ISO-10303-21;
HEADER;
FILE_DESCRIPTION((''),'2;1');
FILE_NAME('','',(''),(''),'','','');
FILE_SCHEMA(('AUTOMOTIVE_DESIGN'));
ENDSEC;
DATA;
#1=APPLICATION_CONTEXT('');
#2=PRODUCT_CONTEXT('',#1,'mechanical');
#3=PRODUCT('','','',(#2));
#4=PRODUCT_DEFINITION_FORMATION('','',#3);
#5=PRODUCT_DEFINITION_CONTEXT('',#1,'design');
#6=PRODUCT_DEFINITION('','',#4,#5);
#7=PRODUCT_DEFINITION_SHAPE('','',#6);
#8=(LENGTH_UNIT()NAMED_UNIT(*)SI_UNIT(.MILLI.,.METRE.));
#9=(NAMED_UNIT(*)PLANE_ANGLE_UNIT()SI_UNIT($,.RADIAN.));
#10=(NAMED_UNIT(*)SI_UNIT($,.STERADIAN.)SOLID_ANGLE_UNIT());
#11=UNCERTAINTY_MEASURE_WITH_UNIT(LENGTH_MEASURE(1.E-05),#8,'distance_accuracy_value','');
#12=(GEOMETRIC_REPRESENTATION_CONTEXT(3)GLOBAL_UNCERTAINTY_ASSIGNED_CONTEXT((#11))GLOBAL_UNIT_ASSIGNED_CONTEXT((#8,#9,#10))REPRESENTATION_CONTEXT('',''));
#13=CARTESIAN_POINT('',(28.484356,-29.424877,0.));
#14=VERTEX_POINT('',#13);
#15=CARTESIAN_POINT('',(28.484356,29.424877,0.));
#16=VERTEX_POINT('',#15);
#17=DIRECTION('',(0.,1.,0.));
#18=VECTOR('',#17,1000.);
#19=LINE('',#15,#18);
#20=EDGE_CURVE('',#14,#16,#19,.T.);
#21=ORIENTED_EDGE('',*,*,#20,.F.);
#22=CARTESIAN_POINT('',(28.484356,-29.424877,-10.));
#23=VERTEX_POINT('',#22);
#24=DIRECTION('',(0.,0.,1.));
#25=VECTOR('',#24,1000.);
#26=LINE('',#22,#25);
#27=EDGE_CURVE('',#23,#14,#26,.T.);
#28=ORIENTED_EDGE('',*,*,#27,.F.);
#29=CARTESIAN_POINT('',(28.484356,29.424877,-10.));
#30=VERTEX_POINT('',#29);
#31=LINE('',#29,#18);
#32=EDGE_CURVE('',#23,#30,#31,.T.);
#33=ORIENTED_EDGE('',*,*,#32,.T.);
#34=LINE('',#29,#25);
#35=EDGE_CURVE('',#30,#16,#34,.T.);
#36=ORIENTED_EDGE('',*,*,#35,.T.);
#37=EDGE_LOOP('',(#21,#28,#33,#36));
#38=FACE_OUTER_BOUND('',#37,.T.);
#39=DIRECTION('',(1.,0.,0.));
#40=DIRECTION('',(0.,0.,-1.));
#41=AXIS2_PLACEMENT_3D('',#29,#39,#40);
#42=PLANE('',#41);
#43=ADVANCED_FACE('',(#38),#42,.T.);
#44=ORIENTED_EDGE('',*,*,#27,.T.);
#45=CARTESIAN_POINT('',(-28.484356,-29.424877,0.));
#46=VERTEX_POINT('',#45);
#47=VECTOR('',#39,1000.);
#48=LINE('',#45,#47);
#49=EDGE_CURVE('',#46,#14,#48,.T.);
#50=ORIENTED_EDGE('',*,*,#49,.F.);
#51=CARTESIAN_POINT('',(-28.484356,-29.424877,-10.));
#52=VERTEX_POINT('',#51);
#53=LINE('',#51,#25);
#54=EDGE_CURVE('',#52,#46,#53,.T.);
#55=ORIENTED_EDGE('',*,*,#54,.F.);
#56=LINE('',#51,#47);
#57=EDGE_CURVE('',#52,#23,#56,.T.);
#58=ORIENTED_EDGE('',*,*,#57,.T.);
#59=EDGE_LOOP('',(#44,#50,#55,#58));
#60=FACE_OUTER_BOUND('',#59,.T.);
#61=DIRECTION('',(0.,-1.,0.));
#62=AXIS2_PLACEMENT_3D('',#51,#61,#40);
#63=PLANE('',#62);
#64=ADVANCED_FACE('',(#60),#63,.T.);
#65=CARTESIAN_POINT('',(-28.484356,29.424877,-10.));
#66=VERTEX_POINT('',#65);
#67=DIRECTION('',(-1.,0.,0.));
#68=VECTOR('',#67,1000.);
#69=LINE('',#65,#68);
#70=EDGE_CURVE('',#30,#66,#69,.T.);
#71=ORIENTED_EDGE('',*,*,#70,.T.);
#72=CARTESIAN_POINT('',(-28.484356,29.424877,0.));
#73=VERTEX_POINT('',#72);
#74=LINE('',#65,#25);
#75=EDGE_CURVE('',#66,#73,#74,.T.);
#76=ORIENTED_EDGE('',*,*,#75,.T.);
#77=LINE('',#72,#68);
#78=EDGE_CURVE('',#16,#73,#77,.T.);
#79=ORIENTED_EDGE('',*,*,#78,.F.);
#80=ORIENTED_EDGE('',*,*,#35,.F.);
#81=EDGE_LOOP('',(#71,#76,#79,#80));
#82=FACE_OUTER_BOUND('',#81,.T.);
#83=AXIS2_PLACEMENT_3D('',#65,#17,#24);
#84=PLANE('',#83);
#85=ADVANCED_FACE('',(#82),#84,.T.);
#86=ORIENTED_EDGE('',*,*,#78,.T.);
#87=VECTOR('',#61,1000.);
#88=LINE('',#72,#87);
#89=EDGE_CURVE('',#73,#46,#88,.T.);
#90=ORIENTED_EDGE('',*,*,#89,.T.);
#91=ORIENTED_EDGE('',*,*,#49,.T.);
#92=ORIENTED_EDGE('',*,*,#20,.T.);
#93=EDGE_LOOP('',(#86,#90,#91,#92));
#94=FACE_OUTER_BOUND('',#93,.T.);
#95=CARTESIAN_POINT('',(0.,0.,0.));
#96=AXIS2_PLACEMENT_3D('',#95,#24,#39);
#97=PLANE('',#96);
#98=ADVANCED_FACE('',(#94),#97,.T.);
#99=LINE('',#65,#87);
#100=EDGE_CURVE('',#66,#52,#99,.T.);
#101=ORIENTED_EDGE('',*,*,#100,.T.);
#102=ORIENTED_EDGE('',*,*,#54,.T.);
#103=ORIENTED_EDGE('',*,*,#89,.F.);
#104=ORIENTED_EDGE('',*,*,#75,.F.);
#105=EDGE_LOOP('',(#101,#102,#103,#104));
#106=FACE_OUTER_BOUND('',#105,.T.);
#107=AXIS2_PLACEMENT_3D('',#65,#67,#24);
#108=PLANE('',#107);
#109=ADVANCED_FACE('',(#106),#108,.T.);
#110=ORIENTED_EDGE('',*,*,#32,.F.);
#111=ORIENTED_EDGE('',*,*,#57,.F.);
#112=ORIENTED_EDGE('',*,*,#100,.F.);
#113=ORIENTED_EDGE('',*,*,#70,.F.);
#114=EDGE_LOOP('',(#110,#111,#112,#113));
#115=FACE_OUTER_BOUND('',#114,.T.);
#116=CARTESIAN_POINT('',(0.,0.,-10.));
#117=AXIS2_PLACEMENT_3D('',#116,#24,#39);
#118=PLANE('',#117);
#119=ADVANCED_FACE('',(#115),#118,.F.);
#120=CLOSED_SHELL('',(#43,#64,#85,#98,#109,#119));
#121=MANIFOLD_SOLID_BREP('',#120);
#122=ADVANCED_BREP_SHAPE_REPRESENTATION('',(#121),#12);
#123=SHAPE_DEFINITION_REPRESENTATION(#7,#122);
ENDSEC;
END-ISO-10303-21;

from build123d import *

# Parameters (mm, degrees)
SKETCH_1_W      = 56.968712564
SKETCH_1_H      = 58.84975496
EXTRUDE_1_DEPTH = 10


with BuildPart() as part:
    # 草图1 → 凸台-拉伸1 (new body)
    with BuildSketch(Plane.XY):
        Rectangle(SKETCH_1_W, SKETCH_1_H)
    extrude(amount=-EXTRUDE_1_DEPTH)


solid = part.part
